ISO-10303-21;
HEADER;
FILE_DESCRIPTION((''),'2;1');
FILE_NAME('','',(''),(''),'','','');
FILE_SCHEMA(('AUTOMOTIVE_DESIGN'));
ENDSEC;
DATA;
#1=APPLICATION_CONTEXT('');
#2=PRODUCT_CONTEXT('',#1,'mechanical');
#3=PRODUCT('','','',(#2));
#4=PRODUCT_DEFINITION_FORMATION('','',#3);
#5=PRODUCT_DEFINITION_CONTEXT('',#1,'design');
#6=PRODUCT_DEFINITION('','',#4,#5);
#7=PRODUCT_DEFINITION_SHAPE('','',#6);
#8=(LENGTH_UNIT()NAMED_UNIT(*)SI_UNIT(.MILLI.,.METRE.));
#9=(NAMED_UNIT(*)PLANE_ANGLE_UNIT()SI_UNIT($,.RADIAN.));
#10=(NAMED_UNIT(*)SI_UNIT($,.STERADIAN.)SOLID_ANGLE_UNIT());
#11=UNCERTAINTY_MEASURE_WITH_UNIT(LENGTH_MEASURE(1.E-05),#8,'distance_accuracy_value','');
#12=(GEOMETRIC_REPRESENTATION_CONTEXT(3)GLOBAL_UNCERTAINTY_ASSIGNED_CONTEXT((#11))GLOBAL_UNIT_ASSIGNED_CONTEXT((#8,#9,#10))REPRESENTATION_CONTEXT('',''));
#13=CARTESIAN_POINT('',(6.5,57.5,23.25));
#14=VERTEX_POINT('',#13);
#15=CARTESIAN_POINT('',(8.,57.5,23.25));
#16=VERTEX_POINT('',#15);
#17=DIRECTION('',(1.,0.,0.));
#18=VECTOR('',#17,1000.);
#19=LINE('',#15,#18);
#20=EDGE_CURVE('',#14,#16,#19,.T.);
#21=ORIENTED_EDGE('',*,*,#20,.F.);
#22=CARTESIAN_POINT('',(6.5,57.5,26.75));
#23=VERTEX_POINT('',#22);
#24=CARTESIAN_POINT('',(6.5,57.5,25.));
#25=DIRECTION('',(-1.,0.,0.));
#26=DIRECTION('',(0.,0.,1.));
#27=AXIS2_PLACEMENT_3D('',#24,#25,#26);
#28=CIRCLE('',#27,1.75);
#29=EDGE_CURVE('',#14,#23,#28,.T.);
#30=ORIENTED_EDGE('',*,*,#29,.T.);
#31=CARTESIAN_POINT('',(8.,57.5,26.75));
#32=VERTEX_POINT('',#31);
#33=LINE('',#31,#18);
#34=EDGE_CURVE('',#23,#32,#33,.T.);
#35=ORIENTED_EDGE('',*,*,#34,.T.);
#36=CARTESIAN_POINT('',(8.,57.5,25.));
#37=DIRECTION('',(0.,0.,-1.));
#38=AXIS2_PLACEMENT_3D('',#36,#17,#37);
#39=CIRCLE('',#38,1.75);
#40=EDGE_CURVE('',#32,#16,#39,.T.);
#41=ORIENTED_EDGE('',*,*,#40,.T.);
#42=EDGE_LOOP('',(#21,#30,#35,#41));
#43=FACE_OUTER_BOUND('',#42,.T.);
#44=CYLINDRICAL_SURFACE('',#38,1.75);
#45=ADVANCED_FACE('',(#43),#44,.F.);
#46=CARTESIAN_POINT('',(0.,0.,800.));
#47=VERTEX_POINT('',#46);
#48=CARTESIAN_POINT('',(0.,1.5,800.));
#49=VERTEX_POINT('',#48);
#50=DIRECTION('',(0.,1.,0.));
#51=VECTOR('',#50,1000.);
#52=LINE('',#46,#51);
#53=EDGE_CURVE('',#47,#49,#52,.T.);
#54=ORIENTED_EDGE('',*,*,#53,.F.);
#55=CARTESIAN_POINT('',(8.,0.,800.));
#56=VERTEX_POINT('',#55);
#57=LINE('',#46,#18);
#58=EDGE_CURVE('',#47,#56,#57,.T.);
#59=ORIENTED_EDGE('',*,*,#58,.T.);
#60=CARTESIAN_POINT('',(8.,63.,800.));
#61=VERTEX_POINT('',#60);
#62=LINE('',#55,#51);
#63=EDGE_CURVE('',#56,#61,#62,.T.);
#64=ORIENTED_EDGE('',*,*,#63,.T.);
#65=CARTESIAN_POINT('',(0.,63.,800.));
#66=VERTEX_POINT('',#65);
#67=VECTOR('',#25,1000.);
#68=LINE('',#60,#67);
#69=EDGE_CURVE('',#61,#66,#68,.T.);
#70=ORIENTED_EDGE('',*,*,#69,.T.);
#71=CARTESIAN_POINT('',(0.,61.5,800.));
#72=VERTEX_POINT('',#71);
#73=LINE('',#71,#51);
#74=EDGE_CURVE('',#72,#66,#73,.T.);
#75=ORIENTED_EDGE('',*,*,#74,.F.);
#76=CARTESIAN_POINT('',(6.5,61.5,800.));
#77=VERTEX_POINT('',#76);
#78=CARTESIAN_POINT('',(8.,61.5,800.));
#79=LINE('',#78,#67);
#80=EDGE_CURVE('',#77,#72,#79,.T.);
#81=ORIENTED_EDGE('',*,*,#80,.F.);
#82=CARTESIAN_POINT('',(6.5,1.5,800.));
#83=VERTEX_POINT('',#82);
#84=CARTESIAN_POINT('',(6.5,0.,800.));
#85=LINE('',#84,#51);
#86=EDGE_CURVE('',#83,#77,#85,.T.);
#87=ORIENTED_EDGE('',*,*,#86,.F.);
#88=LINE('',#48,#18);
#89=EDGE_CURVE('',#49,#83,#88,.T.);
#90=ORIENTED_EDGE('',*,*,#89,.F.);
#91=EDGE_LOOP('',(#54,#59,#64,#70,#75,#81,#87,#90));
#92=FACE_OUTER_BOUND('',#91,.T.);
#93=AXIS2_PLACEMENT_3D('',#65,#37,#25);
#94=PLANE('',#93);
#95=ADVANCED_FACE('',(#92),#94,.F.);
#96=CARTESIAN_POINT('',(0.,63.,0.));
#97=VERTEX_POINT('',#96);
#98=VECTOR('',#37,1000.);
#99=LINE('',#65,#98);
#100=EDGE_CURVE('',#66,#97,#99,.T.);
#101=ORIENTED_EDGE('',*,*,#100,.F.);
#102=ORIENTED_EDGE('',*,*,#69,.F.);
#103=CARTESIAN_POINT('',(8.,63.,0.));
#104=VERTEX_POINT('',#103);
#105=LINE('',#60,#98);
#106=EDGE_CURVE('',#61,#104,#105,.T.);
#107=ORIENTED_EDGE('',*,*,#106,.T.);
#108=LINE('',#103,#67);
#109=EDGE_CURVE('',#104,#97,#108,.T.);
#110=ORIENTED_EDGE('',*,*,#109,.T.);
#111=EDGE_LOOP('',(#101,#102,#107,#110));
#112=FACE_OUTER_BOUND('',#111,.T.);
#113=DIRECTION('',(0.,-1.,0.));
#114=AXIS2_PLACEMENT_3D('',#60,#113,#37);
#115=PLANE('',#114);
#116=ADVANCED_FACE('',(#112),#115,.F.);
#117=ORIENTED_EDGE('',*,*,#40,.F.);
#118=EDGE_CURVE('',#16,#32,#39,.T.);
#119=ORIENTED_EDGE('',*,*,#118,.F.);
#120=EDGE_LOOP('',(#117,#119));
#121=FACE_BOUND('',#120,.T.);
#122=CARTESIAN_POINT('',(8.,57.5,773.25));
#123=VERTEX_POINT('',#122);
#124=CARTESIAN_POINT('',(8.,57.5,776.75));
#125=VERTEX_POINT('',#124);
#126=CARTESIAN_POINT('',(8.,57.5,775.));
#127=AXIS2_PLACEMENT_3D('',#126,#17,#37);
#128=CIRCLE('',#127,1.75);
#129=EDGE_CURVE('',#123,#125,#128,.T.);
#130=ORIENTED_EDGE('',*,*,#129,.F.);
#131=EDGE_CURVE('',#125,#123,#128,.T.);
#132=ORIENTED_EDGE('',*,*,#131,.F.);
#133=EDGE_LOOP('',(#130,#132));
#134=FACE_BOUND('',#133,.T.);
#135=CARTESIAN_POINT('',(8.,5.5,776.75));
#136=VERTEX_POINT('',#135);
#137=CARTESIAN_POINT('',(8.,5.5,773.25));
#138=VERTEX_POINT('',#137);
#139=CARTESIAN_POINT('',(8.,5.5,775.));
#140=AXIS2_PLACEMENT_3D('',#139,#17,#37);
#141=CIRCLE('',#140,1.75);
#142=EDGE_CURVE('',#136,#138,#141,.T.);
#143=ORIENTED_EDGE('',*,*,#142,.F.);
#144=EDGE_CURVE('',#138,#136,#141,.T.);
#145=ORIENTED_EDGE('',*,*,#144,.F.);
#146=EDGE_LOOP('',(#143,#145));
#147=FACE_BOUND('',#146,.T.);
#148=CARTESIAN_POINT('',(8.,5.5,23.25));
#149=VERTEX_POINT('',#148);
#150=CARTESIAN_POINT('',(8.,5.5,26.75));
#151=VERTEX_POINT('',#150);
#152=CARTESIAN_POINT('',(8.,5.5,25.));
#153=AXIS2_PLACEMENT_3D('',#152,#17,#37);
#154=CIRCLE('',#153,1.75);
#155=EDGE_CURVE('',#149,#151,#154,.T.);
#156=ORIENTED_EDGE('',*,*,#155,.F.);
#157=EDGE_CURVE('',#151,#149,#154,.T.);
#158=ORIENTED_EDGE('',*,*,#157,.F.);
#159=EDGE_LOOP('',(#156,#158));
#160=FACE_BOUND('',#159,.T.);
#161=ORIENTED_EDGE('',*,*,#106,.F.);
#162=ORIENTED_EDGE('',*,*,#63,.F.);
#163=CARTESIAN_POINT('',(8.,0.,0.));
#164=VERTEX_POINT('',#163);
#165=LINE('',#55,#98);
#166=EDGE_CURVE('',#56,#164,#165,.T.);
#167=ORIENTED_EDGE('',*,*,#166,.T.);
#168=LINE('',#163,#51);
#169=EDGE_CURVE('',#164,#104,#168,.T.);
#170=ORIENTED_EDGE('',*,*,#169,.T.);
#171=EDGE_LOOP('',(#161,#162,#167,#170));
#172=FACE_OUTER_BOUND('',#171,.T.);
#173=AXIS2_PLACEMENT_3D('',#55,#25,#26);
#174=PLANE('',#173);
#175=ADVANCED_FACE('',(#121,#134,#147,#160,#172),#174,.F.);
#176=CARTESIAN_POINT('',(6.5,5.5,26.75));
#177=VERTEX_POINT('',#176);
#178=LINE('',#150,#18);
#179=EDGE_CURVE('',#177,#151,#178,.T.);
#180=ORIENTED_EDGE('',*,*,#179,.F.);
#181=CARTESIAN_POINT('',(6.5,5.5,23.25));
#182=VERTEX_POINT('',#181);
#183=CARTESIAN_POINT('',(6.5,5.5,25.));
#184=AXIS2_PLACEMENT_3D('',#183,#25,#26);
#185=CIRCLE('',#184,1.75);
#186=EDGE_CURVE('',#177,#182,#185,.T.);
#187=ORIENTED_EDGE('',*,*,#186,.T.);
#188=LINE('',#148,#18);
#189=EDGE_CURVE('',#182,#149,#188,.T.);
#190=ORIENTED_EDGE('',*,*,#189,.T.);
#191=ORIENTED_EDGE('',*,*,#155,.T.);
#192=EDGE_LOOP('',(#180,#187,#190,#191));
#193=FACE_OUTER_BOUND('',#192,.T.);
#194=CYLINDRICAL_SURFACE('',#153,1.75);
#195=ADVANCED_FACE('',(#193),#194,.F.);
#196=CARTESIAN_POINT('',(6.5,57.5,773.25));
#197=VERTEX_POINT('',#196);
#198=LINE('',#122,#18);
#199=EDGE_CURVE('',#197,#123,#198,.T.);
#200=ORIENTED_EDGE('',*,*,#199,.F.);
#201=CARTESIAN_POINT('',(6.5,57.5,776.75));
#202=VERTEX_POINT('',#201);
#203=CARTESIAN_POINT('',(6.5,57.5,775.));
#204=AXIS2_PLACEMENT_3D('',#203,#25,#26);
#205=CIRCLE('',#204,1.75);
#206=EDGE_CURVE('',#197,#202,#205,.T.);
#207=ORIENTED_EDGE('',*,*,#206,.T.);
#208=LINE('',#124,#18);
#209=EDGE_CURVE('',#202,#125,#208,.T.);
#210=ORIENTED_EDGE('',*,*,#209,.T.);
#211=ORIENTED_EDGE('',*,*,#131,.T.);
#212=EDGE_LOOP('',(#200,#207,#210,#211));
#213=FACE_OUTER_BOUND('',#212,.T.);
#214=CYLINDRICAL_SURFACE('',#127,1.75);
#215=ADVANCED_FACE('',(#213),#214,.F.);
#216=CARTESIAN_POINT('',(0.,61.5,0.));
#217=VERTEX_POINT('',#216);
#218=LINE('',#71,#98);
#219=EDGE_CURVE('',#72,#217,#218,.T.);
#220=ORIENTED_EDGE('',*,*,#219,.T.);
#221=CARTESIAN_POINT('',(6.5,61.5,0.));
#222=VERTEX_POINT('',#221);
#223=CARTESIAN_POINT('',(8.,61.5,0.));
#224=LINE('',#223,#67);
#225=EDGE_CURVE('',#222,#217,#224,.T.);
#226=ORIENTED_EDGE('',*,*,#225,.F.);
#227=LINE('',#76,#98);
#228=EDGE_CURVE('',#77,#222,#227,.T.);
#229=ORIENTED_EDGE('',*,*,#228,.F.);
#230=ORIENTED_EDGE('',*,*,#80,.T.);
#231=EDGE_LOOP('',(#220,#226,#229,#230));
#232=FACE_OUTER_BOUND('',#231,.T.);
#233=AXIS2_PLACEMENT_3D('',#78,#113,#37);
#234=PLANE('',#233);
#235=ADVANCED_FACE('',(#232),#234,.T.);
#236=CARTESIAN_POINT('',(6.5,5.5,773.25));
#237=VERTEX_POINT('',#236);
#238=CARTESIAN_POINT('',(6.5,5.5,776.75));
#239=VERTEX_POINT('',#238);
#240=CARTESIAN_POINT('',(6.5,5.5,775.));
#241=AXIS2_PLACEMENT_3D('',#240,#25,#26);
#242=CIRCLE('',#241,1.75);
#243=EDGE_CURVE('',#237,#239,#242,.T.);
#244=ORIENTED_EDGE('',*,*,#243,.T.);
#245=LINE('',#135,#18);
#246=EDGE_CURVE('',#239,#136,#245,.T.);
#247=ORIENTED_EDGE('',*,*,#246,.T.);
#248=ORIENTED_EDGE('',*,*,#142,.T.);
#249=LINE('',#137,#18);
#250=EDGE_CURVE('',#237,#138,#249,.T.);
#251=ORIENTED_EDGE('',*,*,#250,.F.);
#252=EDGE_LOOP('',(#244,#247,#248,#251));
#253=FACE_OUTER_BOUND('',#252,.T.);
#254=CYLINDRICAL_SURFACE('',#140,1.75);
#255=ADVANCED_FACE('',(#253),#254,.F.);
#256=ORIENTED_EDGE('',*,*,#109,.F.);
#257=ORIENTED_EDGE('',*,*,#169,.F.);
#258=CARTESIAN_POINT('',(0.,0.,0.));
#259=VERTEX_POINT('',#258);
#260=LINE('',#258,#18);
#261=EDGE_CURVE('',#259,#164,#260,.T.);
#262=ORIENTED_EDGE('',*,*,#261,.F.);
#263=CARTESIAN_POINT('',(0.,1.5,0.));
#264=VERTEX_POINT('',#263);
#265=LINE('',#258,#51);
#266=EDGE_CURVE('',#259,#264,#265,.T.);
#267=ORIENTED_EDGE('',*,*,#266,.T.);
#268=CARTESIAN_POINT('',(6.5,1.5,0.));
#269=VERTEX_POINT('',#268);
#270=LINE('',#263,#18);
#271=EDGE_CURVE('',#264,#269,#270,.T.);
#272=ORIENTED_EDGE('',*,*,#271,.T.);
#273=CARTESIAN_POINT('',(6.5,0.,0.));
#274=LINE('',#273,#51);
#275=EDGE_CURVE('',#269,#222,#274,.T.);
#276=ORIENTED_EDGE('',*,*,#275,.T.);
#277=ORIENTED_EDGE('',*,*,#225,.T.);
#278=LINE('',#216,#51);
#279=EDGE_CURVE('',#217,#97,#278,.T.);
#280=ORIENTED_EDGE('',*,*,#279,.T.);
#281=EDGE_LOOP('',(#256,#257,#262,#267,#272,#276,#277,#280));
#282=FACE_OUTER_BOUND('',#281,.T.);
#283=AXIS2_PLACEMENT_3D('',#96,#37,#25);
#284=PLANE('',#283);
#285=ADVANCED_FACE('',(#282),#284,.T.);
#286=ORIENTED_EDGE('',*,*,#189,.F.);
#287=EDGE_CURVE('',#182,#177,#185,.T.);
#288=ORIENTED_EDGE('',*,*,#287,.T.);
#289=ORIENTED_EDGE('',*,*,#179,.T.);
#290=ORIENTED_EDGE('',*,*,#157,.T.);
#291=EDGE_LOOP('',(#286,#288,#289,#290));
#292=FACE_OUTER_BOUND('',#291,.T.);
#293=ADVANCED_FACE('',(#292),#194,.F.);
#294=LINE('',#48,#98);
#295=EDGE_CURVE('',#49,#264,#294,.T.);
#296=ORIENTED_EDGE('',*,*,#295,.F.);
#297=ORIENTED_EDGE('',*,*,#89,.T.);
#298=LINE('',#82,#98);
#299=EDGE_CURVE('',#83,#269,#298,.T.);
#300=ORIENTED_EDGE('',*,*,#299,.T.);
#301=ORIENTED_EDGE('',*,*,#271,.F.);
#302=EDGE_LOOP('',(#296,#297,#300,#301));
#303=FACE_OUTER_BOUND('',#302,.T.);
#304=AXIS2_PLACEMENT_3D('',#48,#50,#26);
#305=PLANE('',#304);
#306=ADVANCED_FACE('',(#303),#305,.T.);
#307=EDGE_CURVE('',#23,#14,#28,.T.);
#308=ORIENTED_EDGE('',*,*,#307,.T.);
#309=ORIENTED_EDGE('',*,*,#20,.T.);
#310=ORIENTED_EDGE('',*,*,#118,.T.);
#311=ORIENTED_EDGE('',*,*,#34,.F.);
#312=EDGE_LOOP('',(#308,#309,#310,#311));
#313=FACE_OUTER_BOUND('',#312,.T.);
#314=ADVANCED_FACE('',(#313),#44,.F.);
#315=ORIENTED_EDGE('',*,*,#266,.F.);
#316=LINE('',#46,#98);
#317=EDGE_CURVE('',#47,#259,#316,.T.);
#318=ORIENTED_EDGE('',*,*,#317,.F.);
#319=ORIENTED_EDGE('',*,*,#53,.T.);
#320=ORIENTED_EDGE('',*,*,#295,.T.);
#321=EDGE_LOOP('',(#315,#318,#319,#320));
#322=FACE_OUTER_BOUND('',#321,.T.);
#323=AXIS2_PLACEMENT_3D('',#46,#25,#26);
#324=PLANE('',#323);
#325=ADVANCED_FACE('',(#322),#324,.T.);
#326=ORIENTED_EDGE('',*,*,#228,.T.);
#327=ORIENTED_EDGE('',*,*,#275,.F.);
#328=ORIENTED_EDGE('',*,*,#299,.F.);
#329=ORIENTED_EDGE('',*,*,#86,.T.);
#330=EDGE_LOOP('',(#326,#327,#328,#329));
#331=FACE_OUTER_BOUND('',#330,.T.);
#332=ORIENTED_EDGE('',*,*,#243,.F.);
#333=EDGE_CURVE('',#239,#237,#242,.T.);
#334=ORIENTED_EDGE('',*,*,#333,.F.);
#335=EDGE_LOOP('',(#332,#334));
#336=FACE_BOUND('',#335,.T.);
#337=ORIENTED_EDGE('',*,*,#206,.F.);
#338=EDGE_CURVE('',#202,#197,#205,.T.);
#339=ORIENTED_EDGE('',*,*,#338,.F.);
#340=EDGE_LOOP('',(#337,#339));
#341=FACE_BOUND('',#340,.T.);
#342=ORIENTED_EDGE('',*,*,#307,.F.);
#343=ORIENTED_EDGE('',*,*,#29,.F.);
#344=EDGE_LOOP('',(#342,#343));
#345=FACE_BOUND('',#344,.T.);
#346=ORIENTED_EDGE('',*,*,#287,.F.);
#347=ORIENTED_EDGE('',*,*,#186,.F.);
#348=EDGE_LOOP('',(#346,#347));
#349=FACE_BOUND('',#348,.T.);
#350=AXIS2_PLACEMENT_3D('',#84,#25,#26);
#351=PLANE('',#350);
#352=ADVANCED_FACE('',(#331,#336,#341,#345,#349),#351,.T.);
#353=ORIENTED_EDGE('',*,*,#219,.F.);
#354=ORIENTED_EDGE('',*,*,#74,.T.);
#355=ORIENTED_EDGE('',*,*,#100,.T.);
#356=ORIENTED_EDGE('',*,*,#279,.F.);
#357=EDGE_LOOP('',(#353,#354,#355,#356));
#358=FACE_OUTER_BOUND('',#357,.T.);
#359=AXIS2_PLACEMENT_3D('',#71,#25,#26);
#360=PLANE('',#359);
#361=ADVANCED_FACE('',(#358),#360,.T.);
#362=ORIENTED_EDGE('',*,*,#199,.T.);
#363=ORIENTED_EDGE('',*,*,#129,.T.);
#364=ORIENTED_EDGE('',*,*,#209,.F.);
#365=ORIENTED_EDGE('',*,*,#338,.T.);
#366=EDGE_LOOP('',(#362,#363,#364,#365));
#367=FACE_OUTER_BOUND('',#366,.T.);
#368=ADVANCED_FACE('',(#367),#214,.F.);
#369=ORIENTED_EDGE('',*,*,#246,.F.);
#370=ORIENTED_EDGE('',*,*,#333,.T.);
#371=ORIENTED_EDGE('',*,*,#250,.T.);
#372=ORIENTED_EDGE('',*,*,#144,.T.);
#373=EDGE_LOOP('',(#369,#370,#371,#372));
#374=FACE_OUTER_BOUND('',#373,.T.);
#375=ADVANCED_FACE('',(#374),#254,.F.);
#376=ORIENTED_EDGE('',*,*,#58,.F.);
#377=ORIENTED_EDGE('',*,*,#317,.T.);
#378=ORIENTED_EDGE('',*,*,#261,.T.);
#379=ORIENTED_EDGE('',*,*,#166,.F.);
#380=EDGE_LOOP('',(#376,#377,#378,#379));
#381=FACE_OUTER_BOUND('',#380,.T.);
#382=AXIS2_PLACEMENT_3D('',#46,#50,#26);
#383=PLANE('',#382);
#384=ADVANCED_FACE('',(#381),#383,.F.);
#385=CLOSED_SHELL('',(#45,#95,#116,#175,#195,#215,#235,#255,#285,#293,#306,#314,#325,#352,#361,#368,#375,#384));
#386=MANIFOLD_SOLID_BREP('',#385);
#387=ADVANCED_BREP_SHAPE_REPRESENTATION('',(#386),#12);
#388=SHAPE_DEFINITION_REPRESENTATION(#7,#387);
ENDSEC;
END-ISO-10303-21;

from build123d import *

# Parameters (mm, degrees)
EXTRUDE_1_DEPTH         = 800
HOLE_WIZARD_3_5_3_5_1_D = 3.5


with BuildPart() as part:
    # 草图1 → 拉伸-薄壁1 (new body)
    with BuildSketch(Plane.XY):
        Polygon((0, 0), (8, 0), (8, 63), (0, 63), (0, 61.5), (6.5, 61.5), (6.5, 1.5), (0, 1.5), align=None)
    extrude(amount=EXTRUDE_1_DEPTH)

    # Ø3.5 (3.5) 直径孔1 (through all)
    with Locations(Plane(origin=(8, 0, 0), x_dir=(0, 0, -1), z_dir=(1, 0, 0))):
        with Locations((-775, 57.5), (-25, 57.5)):
            hole_wizard_3_5_3_5_1 = Hole(HOLE_WIZARD_3_5_3_5_1_D / 2)

    # 镜向1: Ø3.5 (3.5) 直径孔1 across plane
    add(hole_wizard_3_5_3_5_1.mirror(Plane(origin=(0, 31.5, 0), x_dir=(0, 0, 1), z_dir=(0, -1, 0))), mode=Mode.SUBTRACT)


solid = part.part
